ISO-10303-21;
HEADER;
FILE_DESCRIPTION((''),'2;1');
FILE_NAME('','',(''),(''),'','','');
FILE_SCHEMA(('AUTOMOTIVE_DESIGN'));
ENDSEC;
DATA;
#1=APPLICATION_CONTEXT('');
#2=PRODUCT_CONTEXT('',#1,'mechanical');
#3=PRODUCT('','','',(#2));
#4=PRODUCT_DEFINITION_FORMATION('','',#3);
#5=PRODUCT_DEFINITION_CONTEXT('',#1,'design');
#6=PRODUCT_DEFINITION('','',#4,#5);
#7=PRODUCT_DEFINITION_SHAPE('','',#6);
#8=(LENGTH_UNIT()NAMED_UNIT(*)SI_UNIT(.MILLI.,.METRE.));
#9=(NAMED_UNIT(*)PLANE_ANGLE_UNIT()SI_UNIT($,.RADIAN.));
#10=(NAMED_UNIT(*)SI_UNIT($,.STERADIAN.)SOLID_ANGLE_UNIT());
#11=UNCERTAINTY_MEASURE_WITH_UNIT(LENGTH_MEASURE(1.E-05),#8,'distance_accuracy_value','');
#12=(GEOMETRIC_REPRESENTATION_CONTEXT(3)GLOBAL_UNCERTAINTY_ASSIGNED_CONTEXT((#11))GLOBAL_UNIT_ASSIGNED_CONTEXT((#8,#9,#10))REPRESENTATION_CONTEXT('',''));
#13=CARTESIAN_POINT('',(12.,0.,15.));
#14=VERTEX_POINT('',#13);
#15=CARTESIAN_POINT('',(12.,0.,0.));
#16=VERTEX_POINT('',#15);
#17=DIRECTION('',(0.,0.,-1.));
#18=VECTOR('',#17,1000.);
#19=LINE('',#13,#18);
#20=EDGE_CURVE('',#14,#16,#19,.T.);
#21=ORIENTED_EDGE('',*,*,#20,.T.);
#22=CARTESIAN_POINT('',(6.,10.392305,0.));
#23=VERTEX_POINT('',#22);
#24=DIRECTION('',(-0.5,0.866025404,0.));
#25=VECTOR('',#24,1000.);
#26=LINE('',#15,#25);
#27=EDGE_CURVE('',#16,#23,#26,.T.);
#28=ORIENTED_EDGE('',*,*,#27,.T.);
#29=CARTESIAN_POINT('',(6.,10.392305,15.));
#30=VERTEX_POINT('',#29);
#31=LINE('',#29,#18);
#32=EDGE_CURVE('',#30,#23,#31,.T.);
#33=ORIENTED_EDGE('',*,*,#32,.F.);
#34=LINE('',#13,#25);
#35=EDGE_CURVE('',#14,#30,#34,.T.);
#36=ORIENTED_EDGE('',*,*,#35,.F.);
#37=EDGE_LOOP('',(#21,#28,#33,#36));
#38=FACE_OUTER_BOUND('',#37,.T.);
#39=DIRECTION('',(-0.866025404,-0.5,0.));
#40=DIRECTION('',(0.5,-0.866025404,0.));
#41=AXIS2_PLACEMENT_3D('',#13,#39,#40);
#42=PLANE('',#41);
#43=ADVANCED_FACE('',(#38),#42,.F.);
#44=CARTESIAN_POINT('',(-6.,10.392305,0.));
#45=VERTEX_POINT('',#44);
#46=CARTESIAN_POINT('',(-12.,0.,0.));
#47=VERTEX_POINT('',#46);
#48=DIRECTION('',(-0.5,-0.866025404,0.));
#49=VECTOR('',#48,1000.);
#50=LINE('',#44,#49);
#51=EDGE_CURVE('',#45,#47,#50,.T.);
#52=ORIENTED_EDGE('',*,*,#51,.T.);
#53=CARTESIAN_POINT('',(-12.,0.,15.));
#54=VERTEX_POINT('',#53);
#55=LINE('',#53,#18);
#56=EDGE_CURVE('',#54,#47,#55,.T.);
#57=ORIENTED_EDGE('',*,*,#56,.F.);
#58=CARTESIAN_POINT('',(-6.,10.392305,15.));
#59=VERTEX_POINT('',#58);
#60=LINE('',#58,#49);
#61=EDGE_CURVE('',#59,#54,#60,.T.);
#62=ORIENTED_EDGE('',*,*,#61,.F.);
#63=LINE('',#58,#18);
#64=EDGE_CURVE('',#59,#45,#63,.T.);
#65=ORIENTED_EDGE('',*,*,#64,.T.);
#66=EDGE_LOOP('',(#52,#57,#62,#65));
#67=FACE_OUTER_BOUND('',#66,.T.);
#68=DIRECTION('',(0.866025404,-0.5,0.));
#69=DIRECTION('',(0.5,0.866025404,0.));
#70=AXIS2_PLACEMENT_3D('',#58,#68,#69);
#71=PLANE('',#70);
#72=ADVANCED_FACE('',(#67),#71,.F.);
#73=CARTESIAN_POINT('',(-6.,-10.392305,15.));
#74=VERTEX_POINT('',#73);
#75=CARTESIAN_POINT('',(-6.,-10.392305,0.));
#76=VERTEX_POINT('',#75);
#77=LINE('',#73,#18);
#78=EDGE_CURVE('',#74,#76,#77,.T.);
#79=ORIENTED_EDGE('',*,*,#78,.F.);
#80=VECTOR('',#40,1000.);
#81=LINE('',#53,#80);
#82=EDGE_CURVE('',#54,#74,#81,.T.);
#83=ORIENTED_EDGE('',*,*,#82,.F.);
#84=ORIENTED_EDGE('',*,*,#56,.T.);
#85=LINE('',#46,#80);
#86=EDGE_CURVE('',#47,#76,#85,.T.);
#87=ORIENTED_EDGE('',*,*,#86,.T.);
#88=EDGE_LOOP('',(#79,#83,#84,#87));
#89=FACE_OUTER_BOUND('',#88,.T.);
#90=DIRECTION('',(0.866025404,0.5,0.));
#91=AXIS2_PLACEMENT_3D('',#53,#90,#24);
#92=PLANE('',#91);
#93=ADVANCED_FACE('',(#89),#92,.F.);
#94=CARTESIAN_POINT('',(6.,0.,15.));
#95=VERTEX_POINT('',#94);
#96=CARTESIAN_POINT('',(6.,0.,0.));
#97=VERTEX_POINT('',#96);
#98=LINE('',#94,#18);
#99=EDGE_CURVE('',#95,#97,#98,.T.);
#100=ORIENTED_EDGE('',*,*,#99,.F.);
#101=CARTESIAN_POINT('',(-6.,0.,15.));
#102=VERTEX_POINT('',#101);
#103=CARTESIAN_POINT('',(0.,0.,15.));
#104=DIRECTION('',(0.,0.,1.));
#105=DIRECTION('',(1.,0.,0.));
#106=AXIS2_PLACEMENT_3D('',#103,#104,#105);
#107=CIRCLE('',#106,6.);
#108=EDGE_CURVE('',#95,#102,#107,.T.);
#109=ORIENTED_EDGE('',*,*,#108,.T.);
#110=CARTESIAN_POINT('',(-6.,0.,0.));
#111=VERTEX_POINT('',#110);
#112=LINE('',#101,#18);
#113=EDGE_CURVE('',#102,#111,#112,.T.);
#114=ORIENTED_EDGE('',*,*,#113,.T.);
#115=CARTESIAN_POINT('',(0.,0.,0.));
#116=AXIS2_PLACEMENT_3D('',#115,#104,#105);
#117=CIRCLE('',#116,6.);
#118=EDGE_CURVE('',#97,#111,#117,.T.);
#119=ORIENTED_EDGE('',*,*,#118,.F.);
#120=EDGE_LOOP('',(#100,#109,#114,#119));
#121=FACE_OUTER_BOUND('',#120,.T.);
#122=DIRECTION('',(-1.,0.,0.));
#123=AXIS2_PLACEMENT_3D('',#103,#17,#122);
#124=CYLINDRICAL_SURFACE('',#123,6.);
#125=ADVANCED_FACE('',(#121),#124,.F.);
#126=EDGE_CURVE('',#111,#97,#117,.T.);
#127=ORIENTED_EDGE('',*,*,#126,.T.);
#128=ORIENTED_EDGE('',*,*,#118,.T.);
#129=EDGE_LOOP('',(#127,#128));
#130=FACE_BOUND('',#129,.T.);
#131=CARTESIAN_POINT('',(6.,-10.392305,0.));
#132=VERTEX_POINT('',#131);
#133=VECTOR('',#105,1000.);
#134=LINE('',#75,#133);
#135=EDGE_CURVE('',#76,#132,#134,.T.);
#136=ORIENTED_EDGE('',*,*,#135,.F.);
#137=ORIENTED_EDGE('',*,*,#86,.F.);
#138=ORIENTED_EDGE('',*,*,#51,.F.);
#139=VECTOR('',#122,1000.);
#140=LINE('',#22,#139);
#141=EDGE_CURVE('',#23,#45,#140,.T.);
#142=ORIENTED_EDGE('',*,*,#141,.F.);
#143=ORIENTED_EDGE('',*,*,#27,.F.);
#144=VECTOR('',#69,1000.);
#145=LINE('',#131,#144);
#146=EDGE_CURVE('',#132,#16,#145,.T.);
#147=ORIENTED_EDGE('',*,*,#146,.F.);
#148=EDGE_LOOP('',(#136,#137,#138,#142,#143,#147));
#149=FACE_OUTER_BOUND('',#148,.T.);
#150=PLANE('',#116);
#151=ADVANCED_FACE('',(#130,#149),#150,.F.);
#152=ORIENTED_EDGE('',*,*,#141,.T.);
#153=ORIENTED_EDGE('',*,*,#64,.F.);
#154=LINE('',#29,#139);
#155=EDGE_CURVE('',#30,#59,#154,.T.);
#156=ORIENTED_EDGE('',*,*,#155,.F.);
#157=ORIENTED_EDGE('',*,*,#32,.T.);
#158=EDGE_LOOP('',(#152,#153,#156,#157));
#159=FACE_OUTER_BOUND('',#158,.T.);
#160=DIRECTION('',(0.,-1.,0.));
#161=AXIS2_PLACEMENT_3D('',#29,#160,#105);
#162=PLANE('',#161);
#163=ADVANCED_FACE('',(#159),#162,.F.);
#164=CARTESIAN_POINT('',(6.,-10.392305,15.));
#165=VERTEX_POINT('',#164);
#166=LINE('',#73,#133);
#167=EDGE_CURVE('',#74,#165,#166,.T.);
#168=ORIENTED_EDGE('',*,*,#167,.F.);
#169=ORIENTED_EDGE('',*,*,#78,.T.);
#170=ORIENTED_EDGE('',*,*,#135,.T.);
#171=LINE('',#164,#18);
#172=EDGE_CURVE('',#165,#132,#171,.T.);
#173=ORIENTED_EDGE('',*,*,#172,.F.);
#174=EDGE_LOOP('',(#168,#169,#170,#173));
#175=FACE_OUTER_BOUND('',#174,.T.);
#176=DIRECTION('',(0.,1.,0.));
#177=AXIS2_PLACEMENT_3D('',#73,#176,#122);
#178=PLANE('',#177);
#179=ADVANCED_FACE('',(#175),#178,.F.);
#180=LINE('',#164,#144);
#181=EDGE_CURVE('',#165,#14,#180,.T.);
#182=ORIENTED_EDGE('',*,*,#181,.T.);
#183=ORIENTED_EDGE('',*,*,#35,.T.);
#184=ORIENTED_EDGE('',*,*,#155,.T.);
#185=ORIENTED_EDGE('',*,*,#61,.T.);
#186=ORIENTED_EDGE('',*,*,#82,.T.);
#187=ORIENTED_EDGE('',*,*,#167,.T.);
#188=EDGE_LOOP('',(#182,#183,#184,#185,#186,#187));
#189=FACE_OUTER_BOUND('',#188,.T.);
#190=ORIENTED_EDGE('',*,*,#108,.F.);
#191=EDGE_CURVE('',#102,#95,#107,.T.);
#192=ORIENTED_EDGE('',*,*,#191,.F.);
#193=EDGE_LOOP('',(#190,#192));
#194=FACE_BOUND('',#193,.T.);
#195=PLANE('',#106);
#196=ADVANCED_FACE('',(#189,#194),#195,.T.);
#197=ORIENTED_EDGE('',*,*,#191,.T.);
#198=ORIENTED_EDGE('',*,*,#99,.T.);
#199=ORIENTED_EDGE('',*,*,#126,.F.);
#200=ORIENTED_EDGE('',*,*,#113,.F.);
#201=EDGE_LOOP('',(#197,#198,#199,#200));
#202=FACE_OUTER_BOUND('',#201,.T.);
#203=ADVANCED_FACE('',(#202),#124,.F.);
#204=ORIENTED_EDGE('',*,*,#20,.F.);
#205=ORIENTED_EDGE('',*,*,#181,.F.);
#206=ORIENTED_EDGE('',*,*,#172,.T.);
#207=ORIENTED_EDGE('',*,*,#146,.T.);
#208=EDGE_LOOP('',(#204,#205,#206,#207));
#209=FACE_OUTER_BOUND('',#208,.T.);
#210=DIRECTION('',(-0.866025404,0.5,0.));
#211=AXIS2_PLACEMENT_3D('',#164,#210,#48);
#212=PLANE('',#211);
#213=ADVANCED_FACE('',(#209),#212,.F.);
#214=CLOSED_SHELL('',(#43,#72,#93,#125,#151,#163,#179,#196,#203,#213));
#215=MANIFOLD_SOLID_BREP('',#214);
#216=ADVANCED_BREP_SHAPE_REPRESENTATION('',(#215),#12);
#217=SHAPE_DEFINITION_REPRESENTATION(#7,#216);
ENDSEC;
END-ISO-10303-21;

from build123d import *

# Parameters (mm, degrees)
HEX_PROFILE_WITH_BORE_12_R = 6
HEX_BODY_15MM_DEPTH        = 15


with BuildPart() as part:
    # Hex Profile with Bore Ø12 → Hex Body 15mm (new body)
    with BuildSketch(Plane.XY):
        Polygon((12, 0), (6, 10.392304845), (-6, 10.392304845), (-12, 0), (-6, -10.392304845), (6, -10.392304845), align=None)
        Circle(HEX_PROFILE_WITH_BORE_12_R, mode=Mode.SUBTRACT)
    extrude(amount=HEX_BODY_15MM_DEPTH)


solid = part.part
